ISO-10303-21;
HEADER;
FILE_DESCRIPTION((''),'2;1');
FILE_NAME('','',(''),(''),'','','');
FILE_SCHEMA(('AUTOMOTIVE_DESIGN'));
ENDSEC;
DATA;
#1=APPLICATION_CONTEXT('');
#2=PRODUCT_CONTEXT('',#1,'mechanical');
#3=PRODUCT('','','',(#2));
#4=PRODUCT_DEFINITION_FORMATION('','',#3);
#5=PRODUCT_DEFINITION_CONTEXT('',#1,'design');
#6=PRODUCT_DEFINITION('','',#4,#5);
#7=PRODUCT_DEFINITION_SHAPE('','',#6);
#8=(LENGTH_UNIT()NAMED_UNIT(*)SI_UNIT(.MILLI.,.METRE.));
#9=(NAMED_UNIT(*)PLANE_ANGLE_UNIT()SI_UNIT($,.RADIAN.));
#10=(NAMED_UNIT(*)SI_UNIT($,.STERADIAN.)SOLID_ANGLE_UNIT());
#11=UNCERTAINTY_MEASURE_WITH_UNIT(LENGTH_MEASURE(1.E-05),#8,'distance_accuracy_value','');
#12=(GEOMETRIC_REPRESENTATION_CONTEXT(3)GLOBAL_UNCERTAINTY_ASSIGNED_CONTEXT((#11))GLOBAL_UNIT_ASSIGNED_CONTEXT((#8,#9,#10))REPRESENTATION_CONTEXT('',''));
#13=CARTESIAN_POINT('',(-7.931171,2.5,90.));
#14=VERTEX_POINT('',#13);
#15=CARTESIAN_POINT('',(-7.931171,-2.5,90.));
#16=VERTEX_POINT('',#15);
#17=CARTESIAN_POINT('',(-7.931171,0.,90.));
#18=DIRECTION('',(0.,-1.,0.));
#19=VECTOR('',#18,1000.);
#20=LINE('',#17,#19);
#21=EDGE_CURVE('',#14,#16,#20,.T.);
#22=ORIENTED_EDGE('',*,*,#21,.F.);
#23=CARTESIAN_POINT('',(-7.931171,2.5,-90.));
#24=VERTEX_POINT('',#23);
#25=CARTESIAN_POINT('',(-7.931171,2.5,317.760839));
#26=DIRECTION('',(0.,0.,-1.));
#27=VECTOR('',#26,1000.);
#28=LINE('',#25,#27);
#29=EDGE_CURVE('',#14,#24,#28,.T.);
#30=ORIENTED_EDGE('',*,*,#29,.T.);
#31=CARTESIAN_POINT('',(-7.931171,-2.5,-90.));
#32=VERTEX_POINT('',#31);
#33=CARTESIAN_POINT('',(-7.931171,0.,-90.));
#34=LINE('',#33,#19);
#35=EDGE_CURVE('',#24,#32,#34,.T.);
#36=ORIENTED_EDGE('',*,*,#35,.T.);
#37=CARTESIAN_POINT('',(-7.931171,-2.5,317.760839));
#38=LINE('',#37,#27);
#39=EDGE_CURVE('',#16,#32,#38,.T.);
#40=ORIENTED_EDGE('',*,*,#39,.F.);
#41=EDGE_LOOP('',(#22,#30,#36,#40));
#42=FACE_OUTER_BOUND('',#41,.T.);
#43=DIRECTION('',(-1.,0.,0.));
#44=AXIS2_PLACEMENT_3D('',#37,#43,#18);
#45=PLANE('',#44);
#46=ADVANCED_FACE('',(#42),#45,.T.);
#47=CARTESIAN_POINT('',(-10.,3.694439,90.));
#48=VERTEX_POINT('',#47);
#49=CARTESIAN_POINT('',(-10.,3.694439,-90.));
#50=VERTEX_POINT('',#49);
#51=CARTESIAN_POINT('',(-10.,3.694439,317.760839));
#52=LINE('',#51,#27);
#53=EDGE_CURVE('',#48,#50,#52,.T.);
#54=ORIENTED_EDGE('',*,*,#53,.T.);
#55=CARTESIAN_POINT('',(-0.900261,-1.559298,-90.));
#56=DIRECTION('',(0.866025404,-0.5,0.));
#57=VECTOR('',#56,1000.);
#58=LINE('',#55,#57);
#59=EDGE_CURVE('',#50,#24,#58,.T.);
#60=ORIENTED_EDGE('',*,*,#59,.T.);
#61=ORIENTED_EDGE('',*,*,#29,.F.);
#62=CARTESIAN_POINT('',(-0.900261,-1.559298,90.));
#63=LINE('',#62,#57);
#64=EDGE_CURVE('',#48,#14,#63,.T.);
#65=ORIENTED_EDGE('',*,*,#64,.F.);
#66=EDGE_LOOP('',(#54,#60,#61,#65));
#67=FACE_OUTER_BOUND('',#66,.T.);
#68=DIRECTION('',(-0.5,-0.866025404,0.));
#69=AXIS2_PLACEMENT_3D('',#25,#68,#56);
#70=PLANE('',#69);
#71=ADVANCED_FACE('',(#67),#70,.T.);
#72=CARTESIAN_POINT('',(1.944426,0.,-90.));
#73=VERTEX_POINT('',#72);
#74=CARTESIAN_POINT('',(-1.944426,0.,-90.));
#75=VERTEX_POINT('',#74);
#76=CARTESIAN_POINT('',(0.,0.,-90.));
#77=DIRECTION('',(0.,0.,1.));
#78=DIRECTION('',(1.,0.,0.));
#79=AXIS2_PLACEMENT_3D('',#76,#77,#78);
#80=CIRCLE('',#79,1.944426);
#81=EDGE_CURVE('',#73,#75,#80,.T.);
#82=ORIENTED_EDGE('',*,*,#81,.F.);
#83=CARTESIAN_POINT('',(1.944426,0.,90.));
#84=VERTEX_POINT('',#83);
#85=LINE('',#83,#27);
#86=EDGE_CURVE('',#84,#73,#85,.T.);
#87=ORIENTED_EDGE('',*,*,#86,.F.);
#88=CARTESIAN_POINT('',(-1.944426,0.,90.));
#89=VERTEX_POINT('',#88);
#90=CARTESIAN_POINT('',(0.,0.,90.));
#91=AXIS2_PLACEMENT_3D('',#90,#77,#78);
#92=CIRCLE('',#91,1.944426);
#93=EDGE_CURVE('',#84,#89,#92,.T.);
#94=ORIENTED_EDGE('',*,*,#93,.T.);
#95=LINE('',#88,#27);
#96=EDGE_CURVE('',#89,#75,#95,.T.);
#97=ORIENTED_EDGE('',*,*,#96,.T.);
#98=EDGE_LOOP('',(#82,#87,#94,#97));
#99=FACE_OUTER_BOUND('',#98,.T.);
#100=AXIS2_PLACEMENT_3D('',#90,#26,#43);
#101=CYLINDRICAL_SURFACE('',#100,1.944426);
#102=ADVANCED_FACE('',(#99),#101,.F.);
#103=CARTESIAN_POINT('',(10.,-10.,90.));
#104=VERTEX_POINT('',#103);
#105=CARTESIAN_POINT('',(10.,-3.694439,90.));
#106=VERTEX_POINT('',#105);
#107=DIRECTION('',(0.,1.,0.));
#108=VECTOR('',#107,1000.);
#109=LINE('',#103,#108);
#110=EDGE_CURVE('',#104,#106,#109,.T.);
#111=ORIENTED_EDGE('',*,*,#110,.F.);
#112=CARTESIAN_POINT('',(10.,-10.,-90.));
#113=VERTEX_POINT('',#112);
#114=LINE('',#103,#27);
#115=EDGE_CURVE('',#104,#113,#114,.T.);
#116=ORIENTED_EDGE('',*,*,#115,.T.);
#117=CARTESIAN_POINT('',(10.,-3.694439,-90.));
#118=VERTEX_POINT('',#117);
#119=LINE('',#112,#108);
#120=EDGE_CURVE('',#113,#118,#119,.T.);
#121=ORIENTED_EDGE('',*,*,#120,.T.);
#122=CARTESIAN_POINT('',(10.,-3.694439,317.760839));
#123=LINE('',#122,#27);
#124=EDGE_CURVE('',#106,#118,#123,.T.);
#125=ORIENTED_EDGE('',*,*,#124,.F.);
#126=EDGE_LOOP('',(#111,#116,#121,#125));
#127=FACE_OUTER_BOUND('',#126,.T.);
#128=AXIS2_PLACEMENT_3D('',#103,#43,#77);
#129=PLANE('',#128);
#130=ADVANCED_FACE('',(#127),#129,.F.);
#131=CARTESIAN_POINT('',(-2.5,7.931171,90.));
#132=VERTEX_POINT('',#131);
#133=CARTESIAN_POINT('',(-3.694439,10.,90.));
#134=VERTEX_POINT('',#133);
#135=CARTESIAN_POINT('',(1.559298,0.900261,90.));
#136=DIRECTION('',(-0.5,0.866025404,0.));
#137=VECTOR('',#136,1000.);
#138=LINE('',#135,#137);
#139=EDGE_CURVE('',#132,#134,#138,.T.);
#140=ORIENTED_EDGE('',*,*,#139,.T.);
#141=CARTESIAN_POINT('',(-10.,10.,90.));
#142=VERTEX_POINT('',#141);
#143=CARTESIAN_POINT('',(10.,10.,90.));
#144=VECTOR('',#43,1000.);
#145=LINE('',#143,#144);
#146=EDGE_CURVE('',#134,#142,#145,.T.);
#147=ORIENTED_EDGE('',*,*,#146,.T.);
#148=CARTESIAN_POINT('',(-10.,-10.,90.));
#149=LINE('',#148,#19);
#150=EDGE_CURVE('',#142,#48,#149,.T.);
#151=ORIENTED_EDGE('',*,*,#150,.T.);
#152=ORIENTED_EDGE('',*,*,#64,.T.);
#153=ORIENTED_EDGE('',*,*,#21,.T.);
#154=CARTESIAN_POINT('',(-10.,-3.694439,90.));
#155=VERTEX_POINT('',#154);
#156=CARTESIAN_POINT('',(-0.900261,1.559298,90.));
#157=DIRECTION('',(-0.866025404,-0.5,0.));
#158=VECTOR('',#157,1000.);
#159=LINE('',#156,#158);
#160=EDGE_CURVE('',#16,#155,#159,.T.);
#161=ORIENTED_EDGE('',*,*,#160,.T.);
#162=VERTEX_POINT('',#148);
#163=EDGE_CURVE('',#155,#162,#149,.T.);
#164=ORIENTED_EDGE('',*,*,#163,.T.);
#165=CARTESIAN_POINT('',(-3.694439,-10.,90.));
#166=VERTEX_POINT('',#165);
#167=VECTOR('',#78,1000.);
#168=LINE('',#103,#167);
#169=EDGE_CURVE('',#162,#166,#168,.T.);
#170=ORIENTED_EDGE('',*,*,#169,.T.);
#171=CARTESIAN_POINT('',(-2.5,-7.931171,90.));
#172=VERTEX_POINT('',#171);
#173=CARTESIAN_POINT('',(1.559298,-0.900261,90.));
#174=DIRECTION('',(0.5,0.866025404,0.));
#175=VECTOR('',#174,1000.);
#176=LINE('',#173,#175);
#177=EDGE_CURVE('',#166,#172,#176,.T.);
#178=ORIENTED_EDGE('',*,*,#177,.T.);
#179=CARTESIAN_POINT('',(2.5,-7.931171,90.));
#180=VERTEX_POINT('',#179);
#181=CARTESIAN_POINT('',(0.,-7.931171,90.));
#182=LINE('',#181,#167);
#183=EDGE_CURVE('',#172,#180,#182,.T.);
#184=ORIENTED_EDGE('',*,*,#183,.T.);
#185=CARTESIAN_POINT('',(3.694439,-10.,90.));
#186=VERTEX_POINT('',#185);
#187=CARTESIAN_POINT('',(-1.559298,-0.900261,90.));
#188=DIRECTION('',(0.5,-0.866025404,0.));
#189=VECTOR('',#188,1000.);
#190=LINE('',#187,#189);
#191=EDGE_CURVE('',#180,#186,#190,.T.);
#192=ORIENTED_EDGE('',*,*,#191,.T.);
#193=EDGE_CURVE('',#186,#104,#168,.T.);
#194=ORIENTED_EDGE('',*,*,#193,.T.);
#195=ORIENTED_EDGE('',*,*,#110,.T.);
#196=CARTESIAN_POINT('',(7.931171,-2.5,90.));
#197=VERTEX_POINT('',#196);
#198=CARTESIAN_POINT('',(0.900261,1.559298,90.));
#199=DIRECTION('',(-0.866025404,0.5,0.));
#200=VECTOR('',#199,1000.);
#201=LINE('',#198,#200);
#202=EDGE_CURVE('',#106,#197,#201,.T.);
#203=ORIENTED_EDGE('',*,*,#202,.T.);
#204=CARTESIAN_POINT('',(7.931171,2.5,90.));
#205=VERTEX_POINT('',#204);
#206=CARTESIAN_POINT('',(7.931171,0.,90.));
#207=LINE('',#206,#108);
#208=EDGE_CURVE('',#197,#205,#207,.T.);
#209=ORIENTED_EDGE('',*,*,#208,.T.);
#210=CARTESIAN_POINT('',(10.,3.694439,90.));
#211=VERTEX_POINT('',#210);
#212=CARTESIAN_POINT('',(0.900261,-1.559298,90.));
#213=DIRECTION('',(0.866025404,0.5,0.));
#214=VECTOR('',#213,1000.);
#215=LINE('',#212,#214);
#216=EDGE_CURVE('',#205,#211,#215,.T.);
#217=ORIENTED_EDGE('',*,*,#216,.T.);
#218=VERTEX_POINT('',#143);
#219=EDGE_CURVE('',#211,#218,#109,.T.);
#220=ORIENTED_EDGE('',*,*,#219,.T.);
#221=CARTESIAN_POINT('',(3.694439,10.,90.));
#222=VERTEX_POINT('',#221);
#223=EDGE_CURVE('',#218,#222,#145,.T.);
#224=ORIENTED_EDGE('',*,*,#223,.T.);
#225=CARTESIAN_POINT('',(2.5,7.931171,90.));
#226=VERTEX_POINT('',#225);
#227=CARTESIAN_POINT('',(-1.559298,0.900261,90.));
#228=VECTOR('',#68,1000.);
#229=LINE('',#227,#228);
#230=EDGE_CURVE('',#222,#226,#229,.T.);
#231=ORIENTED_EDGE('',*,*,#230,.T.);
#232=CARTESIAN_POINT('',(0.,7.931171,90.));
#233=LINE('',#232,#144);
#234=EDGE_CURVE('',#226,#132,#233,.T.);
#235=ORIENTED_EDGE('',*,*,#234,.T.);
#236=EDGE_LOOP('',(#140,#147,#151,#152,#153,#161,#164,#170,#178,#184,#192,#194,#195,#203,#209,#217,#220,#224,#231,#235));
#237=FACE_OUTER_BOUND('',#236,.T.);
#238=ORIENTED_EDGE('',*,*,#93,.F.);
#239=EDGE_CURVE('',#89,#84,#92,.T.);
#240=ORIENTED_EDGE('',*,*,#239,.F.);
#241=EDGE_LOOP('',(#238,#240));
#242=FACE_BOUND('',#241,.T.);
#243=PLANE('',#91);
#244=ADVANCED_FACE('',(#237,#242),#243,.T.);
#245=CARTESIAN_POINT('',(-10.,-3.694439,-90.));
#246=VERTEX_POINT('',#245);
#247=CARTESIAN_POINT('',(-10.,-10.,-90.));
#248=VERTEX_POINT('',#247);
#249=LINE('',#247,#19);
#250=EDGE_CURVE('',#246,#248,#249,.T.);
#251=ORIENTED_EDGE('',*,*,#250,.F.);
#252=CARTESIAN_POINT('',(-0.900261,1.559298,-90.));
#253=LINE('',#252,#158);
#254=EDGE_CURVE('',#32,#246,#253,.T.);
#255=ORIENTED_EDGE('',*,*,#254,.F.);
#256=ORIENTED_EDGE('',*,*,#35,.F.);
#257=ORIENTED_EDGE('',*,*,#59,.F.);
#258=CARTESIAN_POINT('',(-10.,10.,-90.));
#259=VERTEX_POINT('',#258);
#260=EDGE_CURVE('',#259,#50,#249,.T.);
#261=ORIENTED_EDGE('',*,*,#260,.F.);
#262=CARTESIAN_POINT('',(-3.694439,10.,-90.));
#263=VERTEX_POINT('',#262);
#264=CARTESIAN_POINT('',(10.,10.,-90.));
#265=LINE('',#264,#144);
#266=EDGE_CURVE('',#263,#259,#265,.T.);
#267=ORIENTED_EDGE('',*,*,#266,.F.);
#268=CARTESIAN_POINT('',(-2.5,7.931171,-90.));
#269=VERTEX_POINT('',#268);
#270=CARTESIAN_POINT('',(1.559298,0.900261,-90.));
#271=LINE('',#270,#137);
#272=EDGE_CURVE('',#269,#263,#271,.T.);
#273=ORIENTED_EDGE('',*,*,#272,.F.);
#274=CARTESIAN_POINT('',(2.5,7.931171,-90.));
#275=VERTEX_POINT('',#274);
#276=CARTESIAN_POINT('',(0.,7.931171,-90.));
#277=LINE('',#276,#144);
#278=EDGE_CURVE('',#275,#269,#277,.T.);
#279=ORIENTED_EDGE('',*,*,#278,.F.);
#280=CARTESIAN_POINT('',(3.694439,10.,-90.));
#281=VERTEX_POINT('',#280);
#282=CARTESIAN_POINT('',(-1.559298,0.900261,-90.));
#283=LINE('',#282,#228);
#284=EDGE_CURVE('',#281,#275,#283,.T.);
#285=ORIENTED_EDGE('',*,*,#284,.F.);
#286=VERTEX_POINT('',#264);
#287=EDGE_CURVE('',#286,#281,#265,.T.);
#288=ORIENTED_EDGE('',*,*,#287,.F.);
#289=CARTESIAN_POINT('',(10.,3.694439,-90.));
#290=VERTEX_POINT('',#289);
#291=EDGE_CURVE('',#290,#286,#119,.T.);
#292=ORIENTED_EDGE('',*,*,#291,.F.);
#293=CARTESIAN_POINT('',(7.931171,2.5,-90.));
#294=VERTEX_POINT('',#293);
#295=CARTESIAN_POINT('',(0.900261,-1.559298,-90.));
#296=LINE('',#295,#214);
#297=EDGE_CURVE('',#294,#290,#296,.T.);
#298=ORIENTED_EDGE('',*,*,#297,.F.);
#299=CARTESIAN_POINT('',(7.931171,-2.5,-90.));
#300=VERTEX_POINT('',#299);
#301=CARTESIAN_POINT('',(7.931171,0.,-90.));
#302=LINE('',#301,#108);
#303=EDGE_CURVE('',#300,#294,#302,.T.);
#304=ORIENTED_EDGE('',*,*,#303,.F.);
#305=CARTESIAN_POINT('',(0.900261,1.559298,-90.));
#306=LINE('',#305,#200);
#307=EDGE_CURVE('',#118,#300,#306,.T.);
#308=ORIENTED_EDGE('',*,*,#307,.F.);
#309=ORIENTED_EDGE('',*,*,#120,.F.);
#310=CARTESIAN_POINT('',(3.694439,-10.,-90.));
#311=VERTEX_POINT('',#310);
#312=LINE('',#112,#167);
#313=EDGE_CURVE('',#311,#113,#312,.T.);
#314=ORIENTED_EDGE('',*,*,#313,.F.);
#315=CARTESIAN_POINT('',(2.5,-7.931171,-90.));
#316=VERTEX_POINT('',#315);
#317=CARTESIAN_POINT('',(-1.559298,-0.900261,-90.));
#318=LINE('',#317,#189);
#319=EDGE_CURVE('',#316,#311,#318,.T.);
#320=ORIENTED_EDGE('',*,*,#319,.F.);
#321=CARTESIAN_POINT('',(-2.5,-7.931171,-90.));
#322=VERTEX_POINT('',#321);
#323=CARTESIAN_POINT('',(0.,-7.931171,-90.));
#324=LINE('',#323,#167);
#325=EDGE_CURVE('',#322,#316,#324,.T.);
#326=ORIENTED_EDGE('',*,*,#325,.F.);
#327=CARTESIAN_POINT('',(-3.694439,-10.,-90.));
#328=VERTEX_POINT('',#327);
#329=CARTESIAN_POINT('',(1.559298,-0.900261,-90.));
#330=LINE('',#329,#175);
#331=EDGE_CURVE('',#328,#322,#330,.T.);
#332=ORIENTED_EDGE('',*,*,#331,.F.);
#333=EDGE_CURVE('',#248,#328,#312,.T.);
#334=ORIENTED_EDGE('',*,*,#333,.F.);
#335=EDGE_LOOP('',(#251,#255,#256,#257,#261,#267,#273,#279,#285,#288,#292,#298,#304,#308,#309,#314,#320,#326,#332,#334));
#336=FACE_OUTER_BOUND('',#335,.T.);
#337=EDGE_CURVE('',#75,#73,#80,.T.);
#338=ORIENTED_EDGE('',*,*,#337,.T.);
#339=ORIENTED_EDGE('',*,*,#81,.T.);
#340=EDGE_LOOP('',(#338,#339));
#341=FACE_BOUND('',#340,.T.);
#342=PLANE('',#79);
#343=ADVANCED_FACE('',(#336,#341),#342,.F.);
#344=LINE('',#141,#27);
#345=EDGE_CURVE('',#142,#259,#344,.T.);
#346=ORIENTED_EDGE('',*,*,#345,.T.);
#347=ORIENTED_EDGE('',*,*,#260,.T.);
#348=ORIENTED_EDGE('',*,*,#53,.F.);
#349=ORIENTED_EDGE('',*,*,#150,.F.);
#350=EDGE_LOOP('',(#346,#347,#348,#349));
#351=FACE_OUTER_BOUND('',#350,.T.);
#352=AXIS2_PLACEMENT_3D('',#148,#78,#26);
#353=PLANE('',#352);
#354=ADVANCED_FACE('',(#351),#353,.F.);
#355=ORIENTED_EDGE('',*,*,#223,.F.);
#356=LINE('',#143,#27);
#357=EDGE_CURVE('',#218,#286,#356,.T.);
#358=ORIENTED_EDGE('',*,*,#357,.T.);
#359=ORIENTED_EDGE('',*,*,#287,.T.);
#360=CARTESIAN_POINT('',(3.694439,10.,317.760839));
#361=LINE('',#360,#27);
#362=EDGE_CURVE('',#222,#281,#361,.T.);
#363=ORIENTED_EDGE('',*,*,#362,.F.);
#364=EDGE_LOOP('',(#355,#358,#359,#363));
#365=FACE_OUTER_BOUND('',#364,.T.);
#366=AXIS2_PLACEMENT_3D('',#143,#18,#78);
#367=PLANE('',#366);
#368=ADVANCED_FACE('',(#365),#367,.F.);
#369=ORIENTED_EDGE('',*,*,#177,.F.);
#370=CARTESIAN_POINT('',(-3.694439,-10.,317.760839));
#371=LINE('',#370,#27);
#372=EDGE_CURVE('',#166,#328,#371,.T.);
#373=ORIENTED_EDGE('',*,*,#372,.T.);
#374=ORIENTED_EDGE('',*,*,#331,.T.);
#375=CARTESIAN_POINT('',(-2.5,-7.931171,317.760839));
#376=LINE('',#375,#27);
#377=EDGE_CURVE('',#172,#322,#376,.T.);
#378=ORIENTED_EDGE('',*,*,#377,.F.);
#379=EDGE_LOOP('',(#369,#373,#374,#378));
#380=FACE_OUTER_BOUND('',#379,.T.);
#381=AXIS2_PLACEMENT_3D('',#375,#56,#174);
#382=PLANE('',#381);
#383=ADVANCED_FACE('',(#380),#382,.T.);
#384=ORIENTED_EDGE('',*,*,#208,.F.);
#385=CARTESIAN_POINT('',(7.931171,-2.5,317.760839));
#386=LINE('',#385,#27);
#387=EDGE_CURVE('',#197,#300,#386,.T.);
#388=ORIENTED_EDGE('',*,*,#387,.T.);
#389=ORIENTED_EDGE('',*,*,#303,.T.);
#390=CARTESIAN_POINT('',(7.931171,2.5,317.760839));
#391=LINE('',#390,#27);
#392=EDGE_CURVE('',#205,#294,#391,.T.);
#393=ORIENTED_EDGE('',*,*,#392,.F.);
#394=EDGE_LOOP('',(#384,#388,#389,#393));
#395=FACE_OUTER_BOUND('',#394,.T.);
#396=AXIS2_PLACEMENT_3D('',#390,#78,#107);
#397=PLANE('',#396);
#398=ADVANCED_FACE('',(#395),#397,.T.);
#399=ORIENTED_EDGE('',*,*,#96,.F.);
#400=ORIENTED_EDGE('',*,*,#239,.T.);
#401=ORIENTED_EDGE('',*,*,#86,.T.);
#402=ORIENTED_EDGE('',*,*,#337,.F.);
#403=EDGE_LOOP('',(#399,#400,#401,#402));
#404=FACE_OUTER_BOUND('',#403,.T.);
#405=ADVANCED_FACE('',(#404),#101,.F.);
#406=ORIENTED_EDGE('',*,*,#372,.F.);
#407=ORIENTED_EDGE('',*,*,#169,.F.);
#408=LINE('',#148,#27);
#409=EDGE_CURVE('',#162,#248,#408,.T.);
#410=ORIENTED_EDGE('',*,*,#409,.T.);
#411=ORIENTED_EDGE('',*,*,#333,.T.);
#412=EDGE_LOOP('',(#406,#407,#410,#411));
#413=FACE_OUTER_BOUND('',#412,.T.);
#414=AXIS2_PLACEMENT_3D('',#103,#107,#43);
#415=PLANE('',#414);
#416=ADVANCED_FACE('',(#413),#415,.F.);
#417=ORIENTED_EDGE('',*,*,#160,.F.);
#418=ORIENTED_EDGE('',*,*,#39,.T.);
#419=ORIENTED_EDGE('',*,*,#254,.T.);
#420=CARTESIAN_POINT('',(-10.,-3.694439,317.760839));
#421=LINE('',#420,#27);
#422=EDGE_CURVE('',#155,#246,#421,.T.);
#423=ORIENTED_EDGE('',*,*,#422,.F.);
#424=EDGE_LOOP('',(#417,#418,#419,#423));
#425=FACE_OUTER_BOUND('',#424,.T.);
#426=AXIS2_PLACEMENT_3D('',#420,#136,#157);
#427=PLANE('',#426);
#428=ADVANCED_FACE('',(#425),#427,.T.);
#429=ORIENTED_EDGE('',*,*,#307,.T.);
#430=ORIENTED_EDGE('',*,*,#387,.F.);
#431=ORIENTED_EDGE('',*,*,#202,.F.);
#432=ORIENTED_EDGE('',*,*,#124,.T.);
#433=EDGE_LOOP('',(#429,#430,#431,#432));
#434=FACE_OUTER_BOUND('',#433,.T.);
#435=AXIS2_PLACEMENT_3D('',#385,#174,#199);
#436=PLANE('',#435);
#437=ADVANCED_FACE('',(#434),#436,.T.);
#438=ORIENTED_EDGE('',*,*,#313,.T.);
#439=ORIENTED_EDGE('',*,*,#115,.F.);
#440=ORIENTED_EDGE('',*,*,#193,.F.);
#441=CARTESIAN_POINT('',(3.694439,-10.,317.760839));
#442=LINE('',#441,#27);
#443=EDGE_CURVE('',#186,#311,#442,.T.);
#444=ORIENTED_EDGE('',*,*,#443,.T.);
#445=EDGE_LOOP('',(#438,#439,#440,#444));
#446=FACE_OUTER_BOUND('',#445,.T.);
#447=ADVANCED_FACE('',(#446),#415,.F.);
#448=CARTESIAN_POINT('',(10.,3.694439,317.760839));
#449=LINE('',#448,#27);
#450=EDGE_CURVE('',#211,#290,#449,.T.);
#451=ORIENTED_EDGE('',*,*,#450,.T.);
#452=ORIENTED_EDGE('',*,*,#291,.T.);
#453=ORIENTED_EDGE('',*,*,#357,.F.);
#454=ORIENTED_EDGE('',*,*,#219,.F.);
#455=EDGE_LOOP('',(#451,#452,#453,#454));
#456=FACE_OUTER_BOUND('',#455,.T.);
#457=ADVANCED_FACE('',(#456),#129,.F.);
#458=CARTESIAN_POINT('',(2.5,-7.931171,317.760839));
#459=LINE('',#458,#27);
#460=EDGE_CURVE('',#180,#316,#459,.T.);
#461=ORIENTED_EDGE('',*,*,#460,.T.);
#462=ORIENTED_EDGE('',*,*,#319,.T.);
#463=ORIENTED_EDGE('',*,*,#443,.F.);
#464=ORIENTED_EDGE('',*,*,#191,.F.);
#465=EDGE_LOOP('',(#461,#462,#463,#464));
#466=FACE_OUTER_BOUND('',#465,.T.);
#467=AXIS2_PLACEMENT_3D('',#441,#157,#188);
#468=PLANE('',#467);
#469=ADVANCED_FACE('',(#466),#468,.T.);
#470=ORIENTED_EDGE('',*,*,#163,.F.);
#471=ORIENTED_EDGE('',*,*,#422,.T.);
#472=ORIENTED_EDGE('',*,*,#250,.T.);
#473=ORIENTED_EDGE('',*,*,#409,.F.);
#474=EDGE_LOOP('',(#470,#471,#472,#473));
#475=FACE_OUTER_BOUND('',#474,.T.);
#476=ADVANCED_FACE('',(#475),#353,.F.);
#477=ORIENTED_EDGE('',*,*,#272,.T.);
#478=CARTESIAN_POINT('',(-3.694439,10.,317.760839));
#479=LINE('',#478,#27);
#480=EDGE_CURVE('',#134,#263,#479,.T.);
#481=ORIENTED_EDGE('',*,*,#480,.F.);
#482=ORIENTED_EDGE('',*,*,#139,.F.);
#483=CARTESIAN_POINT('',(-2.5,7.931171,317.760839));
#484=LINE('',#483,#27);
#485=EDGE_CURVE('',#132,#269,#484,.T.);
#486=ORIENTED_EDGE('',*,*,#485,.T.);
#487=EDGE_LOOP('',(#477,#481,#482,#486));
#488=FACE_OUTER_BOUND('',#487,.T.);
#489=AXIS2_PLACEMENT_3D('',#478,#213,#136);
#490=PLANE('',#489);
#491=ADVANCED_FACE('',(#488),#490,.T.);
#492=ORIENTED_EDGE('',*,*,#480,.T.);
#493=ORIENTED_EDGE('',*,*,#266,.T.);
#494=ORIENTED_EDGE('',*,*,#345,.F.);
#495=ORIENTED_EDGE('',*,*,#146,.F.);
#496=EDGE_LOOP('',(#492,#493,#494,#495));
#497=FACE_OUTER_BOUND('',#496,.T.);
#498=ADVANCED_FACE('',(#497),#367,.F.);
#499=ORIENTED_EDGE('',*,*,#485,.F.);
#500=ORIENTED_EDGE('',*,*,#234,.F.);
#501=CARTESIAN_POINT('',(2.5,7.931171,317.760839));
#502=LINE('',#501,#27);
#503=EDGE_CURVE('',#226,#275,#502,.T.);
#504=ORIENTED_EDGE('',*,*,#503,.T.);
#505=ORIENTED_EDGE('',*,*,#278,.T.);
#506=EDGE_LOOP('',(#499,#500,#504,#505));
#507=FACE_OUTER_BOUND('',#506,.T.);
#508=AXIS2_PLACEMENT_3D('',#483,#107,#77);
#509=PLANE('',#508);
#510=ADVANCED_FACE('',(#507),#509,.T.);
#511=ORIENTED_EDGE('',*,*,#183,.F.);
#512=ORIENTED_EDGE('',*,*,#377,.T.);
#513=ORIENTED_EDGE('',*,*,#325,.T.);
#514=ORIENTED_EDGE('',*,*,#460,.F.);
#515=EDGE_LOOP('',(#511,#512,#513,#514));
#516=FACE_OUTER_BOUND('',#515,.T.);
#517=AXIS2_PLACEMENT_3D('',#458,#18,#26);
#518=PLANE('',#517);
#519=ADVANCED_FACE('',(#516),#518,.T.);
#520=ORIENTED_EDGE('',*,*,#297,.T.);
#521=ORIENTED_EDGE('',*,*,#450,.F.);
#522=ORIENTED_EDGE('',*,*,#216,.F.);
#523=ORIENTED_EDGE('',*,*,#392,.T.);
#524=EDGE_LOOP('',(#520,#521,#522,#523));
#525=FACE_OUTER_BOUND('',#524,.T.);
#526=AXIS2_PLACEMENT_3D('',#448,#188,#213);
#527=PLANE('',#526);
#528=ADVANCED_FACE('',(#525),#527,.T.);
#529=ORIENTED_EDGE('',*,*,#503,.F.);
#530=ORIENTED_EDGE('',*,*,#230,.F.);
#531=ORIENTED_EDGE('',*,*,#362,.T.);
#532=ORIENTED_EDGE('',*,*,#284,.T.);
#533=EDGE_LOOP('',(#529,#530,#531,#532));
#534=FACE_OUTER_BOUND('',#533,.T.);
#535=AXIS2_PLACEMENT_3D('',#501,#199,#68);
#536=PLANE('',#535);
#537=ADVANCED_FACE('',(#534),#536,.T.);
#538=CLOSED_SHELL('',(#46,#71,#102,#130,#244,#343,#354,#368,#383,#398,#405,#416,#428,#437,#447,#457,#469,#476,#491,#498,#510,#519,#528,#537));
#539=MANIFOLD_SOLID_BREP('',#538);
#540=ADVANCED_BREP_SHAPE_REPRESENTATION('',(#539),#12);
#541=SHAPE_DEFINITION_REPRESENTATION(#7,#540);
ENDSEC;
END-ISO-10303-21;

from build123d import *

# Parameters (mm, degrees)
SKETCH_1_W               = 20
SKETCH_1_H               = 20
SKETCH_1_R               = 1.94442565
EXTRUDE_1_DEPTH          = 90
CUT_EXTRUDE_1_DEPTH      = 181.554700853
PATTERN_CIRCULAR_1_COUNT = 4


with BuildPart() as part:
    # 草图1 → 凸台-拉伸1 (new, symmetric)
    with BuildSketch(Plane.XY):
        Rectangle(SKETCH_1_W, SKETCH_1_H)
        with Locations(Location((0, 0, 0), (0, 0, 180))):
            Circle(SKETCH_1_R, mode=Mode.SUBTRACT)
    extrude(amount=EXTRUDE_1_DEPTH, both=True)

    # 草图2 → 切除-拉伸1 (cut, symmetric)
    with BuildSketch(Plane.XY.offset(90)):
        Polygon((-32.933615203, 60.643738676), (-3.694439046, 10), (-2.5, 7.931170886), (2.5, 7.931170886), (3.694439046, 10), (32.933615203, 60.643738676), (32.933615203, 177.600443305), (-32.933615203, 177.600443305), align=None)
    cut_extrude_1 = extrude(amount=CUT_EXTRUDE_1_DEPTH, both=True, mode=Mode.SUBTRACT)

    # 阵列(圆周)1: 切除-拉伸1 ×4 about axis
    pattern_circular_1_axis = Axis((0, 0, 90), (0, 0, -1))
    for i in range(1, PATTERN_CIRCULAR_1_COUNT):
        add(cut_extrude_1.rotate(pattern_circular_1_axis, i * 360 / PATTERN_CIRCULAR_1_COUNT), mode=Mode.SUBTRACT)


solid = part.part
